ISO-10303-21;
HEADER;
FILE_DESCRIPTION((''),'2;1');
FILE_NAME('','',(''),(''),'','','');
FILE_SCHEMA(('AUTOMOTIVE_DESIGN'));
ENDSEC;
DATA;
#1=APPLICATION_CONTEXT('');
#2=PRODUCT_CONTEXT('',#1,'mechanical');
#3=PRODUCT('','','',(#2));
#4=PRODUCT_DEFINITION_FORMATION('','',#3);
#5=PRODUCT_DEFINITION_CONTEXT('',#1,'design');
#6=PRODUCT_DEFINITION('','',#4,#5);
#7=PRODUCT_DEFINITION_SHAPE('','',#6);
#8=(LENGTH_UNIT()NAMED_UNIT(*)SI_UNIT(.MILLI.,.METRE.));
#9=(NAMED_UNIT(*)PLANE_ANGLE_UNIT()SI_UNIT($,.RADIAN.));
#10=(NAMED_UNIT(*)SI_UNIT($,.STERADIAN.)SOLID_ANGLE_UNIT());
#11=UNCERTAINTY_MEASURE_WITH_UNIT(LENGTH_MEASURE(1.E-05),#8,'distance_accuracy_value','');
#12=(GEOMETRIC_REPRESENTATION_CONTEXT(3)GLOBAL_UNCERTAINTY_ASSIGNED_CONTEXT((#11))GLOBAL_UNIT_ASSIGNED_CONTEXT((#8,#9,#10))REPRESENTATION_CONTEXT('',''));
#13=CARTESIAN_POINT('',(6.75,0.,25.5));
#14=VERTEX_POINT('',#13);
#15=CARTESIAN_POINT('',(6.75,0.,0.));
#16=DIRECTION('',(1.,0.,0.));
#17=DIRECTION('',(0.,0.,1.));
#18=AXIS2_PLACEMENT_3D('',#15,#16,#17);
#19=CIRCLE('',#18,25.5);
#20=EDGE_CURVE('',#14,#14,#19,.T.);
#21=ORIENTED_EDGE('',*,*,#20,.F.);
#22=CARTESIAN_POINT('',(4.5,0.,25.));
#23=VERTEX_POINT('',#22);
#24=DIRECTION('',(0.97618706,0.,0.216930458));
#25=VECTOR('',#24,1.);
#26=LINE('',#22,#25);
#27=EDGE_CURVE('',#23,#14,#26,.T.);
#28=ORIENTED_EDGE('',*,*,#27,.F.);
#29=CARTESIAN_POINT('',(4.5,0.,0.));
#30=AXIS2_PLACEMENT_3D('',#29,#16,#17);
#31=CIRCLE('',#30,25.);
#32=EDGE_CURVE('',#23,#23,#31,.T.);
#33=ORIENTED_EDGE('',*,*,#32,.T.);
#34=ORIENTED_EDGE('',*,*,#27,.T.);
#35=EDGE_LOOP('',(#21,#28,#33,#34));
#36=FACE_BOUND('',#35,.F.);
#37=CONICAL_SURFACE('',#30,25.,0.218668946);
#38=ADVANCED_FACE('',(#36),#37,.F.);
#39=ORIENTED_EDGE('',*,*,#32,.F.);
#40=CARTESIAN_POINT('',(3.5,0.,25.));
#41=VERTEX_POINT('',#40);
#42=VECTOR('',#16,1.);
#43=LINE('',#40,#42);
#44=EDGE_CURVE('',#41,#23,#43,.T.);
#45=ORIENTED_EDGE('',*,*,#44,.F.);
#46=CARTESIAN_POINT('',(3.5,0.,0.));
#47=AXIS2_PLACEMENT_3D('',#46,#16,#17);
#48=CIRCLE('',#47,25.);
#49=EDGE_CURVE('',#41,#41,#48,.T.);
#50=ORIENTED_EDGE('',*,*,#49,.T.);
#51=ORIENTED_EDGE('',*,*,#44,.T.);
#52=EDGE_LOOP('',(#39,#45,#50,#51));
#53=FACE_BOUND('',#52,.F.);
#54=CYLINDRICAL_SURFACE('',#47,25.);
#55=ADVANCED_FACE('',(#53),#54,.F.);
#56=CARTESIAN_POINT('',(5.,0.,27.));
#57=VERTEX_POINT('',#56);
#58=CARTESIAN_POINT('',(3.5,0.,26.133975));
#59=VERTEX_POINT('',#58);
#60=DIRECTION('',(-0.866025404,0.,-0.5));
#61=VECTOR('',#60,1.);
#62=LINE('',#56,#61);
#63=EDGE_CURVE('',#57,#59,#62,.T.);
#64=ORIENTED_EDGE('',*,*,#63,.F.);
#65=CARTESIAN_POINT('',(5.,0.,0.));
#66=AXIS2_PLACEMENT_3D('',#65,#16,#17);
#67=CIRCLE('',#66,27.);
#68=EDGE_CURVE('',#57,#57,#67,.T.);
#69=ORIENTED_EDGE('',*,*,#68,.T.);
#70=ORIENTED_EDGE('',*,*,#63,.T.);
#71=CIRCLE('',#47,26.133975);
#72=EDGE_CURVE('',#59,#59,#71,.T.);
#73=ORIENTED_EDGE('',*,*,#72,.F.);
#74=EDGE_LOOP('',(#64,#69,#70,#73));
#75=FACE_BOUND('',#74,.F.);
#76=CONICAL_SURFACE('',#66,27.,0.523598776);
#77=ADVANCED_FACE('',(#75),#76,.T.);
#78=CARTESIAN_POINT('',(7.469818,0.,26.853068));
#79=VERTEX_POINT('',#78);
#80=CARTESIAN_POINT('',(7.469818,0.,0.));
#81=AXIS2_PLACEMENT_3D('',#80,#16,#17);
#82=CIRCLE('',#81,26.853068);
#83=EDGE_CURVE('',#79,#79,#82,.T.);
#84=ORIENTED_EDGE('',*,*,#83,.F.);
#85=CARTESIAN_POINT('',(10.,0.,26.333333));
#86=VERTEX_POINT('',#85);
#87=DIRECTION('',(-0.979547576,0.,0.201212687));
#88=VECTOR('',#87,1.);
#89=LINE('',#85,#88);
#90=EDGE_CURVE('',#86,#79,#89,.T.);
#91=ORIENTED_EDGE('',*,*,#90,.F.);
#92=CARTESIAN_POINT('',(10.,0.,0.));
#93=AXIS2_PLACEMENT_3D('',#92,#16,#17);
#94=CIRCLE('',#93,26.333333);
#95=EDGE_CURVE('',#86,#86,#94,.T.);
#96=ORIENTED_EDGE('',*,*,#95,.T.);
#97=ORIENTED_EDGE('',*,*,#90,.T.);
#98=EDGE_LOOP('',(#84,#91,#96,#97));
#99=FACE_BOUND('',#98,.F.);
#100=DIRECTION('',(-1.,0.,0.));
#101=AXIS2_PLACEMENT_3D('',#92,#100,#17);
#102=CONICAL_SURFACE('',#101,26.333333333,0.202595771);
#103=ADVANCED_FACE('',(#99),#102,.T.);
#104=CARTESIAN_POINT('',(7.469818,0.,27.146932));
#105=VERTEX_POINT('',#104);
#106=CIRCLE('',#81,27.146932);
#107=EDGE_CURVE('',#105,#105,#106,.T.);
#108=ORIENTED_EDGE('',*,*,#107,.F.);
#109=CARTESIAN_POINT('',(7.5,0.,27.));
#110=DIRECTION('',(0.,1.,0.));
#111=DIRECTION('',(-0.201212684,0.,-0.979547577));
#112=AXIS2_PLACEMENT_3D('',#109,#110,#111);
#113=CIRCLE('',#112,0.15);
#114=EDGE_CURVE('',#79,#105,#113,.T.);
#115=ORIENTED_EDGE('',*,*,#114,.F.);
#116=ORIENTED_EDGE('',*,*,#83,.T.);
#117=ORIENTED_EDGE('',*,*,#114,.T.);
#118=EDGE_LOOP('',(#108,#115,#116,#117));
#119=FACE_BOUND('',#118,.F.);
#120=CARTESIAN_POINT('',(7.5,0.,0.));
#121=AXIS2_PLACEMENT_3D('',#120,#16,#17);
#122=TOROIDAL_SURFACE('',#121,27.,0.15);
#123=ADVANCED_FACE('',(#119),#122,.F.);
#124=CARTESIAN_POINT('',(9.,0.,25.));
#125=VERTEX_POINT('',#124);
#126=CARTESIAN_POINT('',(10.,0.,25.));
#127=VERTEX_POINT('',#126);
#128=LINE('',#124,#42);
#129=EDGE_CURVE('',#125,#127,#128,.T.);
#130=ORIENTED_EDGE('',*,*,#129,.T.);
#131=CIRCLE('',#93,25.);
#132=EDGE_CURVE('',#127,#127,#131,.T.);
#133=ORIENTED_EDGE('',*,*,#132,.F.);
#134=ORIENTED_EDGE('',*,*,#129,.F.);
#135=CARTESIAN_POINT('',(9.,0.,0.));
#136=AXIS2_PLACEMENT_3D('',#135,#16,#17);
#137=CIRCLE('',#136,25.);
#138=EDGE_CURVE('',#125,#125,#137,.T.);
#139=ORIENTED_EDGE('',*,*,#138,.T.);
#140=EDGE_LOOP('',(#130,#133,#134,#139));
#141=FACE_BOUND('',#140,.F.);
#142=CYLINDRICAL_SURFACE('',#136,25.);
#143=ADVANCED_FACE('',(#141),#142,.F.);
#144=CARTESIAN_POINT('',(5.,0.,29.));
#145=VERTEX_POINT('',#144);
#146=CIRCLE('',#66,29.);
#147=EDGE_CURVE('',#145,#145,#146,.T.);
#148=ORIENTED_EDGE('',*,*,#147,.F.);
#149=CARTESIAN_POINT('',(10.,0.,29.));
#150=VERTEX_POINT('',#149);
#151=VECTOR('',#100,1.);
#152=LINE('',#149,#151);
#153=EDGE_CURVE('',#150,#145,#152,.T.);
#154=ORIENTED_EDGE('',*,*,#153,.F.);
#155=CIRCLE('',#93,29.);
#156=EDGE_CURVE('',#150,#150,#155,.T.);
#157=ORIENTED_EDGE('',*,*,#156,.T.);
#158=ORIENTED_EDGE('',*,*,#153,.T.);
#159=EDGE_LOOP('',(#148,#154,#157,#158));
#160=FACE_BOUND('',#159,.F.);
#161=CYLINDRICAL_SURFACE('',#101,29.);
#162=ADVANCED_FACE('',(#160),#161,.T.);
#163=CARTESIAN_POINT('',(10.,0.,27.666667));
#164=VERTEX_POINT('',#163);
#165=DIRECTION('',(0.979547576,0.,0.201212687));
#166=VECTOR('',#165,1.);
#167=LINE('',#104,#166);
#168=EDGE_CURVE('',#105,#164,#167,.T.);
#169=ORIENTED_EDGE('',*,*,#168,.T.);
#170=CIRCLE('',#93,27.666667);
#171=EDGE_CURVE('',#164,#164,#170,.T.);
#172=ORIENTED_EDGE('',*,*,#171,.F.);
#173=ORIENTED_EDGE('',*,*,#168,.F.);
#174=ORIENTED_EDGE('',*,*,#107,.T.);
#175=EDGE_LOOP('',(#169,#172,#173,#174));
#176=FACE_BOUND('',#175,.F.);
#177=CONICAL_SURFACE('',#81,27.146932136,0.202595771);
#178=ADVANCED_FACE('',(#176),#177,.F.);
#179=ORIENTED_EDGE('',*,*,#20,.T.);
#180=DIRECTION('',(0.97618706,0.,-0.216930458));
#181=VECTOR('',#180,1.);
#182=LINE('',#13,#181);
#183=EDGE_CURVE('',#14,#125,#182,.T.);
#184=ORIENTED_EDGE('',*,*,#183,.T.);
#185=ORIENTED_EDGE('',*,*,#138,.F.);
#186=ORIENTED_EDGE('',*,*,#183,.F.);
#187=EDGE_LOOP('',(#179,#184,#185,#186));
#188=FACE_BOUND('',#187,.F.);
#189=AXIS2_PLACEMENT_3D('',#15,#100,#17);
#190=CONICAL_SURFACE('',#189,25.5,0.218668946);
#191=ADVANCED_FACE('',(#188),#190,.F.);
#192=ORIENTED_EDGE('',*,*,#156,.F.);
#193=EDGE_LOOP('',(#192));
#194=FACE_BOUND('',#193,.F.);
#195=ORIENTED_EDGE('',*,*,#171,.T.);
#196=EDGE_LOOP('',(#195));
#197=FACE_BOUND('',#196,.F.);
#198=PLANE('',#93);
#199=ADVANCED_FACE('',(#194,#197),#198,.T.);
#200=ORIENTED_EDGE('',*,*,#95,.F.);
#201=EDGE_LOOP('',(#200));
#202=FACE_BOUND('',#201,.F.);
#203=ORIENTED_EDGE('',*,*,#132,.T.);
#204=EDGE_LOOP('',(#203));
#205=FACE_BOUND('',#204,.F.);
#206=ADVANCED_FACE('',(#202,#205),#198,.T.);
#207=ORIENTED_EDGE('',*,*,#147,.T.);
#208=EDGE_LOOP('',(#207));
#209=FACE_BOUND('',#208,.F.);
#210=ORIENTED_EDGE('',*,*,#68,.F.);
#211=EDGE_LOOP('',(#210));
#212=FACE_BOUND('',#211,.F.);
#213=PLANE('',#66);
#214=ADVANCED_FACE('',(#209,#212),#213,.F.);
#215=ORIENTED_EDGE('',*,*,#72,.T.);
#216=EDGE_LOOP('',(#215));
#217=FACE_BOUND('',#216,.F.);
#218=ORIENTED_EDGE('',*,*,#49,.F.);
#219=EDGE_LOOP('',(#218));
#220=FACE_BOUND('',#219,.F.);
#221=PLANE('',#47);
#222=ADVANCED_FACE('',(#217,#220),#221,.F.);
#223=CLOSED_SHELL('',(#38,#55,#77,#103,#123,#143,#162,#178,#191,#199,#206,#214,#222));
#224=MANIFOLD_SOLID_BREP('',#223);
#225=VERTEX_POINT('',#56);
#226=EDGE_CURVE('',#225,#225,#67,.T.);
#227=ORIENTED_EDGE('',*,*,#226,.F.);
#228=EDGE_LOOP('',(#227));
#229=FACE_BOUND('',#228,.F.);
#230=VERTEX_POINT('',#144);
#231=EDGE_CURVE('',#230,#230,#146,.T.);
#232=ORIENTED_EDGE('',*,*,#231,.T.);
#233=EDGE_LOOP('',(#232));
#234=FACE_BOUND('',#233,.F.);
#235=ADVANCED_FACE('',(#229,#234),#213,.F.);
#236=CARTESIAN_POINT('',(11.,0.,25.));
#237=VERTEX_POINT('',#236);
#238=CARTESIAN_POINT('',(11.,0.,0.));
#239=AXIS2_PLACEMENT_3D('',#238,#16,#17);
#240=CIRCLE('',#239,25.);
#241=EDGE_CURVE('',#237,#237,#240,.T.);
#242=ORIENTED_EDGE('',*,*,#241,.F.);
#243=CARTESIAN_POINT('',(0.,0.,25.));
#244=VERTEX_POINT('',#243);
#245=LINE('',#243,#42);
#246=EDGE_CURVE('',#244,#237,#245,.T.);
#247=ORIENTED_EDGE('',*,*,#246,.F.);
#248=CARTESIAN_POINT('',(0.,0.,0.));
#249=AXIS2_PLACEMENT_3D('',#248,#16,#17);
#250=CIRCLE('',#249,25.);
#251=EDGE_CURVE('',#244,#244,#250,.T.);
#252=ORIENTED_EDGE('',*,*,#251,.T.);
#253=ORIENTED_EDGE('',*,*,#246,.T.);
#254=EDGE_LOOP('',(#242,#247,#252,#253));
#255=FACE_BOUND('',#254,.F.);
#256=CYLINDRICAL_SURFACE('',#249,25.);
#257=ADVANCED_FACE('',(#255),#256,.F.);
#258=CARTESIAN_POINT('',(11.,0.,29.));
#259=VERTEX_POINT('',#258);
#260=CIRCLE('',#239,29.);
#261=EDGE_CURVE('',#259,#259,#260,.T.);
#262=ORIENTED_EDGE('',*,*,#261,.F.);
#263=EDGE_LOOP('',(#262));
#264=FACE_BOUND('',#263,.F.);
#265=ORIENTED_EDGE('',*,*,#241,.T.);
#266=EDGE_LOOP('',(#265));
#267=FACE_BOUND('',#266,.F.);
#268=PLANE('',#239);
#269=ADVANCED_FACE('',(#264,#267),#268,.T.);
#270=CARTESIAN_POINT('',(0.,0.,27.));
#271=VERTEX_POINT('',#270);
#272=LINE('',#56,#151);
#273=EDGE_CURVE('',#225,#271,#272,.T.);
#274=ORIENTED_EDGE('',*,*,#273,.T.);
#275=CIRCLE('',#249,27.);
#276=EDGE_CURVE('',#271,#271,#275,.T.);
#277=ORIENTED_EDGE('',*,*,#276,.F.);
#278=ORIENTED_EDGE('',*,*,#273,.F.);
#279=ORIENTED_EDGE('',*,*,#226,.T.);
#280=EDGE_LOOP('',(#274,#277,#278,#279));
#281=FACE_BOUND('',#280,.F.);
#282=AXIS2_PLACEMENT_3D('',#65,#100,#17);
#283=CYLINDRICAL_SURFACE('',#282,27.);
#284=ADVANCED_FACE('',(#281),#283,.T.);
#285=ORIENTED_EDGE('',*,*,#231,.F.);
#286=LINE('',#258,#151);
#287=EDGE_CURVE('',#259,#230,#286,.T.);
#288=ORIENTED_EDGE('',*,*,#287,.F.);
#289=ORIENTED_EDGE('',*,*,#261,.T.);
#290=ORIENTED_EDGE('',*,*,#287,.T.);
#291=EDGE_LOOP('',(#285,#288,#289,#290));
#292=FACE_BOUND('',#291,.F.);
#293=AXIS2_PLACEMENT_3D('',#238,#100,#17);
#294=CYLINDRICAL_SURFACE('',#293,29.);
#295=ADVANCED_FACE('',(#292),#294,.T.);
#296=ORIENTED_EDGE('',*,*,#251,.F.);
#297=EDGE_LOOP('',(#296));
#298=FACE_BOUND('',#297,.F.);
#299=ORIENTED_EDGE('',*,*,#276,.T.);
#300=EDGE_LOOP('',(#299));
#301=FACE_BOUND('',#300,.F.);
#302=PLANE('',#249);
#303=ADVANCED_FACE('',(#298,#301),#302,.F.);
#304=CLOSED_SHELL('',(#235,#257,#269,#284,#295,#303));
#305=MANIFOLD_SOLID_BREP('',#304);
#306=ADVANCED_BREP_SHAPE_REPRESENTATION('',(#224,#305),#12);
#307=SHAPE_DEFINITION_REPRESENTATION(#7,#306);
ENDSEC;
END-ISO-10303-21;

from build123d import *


with BuildPart() as part:
    # 草图1 → 旋转1 (revolve)
    with BuildSketch(Plane.XY, mode=Mode.PRIVATE) as revolve_1_sk:
        with BuildLine():
            Line((10, 29), (5, 29))
            Line((5, 29), (5, 27))
            Line((5, 27), (3.5, 26.133974596))
            Line((3.5, 26.133974596), (3.5, 25))
            Line((3.5, 25), (4.5, 25))
            Line((4.5, 25), (6.75, 25.5))
            Line((6.75, 25.5), (9, 25))
            Line((9, 25), (10, 25))
            Line((10, 25), (10, 26.333333333))
            Line((10, 26.333333333), (7.469818097, 26.853067864))
            ThreePointArc((7.469818097, 26.853067864), (7.35, 27), (7.469818097, 27.146932136))
            Line((7.469818097, 27.146932136), (10, 27.666666667))
            Line((10, 27.666666667), (10, 29))
        make_face()
    revolve(revolve_1_sk.sketch.rotate(Axis((0, 0, 0), (1, 0, 0)), 90), axis=Axis((0, 0, 0), (1, 0, 0)))


with BuildPart() as body_2:
    # 草图1<3> → 旋转2 (revolve)
    with BuildSketch(Plane.XY, mode=Mode.PRIVATE) as revolve_2_sk:
        Polygon((3.5, 26.133974596), (3.5, 27), (0, 27), (0, 25), (3.5, 25), align=None)
        Polygon((3.5, 26.133974596), (5, 27), (3.5, 27), align=None)
        Polygon((6.75, 25.5), (4.5, 25), (9, 25), align=None)
        with BuildLine():
            Line((10, 26.333333333), (10, 27.666666667))
            Line((10, 27.666666667), (7.469818097, 27.146932136))
            ThreePointArc((7.469818097, 27.146932136), (7.35, 27), (7.469818097, 26.853067864))
            Line((7.469818097, 26.853067864), (10, 26.333333333))
        make_face()
        with BuildLine():
            Line((10, 29), (5, 29))
            Line((5, 29), (5, 27))
            Line((5, 27), (3.5, 26.133974596))
            Line((3.5, 26.133974596), (3.5, 25))
            Line((3.5, 25), (4.5, 25))
            Line((4.5, 25), (6.75, 25.5))
            Line((6.75, 25.5), (9, 25))
            Line((9, 25), (10, 25))
            Line((10, 25), (10, 26.333333333))
            Line((10, 26.333333333), (7.469818097, 26.853067864))
            ThreePointArc((7.469818097, 26.853067864), (7.35, 27), (7.469818097, 27.146932136))
            Line((7.469818097, 27.146932136), (10, 27.666666667))
            Line((10, 27.666666667), (10, 29))
        make_face()
        Polygon((11, 29), (10, 29), (10, 27.666666667), (10, 26.333333333), (10, 25), (11, 25), align=None)
    revolve(revolve_2_sk.sketch.rotate(Axis((0, 0, 0), (1, 0, 0)), 90), axis=Axis((0, 0, 0), (1, 0, 0)))


solid = Compound([part.part, body_2.part])
